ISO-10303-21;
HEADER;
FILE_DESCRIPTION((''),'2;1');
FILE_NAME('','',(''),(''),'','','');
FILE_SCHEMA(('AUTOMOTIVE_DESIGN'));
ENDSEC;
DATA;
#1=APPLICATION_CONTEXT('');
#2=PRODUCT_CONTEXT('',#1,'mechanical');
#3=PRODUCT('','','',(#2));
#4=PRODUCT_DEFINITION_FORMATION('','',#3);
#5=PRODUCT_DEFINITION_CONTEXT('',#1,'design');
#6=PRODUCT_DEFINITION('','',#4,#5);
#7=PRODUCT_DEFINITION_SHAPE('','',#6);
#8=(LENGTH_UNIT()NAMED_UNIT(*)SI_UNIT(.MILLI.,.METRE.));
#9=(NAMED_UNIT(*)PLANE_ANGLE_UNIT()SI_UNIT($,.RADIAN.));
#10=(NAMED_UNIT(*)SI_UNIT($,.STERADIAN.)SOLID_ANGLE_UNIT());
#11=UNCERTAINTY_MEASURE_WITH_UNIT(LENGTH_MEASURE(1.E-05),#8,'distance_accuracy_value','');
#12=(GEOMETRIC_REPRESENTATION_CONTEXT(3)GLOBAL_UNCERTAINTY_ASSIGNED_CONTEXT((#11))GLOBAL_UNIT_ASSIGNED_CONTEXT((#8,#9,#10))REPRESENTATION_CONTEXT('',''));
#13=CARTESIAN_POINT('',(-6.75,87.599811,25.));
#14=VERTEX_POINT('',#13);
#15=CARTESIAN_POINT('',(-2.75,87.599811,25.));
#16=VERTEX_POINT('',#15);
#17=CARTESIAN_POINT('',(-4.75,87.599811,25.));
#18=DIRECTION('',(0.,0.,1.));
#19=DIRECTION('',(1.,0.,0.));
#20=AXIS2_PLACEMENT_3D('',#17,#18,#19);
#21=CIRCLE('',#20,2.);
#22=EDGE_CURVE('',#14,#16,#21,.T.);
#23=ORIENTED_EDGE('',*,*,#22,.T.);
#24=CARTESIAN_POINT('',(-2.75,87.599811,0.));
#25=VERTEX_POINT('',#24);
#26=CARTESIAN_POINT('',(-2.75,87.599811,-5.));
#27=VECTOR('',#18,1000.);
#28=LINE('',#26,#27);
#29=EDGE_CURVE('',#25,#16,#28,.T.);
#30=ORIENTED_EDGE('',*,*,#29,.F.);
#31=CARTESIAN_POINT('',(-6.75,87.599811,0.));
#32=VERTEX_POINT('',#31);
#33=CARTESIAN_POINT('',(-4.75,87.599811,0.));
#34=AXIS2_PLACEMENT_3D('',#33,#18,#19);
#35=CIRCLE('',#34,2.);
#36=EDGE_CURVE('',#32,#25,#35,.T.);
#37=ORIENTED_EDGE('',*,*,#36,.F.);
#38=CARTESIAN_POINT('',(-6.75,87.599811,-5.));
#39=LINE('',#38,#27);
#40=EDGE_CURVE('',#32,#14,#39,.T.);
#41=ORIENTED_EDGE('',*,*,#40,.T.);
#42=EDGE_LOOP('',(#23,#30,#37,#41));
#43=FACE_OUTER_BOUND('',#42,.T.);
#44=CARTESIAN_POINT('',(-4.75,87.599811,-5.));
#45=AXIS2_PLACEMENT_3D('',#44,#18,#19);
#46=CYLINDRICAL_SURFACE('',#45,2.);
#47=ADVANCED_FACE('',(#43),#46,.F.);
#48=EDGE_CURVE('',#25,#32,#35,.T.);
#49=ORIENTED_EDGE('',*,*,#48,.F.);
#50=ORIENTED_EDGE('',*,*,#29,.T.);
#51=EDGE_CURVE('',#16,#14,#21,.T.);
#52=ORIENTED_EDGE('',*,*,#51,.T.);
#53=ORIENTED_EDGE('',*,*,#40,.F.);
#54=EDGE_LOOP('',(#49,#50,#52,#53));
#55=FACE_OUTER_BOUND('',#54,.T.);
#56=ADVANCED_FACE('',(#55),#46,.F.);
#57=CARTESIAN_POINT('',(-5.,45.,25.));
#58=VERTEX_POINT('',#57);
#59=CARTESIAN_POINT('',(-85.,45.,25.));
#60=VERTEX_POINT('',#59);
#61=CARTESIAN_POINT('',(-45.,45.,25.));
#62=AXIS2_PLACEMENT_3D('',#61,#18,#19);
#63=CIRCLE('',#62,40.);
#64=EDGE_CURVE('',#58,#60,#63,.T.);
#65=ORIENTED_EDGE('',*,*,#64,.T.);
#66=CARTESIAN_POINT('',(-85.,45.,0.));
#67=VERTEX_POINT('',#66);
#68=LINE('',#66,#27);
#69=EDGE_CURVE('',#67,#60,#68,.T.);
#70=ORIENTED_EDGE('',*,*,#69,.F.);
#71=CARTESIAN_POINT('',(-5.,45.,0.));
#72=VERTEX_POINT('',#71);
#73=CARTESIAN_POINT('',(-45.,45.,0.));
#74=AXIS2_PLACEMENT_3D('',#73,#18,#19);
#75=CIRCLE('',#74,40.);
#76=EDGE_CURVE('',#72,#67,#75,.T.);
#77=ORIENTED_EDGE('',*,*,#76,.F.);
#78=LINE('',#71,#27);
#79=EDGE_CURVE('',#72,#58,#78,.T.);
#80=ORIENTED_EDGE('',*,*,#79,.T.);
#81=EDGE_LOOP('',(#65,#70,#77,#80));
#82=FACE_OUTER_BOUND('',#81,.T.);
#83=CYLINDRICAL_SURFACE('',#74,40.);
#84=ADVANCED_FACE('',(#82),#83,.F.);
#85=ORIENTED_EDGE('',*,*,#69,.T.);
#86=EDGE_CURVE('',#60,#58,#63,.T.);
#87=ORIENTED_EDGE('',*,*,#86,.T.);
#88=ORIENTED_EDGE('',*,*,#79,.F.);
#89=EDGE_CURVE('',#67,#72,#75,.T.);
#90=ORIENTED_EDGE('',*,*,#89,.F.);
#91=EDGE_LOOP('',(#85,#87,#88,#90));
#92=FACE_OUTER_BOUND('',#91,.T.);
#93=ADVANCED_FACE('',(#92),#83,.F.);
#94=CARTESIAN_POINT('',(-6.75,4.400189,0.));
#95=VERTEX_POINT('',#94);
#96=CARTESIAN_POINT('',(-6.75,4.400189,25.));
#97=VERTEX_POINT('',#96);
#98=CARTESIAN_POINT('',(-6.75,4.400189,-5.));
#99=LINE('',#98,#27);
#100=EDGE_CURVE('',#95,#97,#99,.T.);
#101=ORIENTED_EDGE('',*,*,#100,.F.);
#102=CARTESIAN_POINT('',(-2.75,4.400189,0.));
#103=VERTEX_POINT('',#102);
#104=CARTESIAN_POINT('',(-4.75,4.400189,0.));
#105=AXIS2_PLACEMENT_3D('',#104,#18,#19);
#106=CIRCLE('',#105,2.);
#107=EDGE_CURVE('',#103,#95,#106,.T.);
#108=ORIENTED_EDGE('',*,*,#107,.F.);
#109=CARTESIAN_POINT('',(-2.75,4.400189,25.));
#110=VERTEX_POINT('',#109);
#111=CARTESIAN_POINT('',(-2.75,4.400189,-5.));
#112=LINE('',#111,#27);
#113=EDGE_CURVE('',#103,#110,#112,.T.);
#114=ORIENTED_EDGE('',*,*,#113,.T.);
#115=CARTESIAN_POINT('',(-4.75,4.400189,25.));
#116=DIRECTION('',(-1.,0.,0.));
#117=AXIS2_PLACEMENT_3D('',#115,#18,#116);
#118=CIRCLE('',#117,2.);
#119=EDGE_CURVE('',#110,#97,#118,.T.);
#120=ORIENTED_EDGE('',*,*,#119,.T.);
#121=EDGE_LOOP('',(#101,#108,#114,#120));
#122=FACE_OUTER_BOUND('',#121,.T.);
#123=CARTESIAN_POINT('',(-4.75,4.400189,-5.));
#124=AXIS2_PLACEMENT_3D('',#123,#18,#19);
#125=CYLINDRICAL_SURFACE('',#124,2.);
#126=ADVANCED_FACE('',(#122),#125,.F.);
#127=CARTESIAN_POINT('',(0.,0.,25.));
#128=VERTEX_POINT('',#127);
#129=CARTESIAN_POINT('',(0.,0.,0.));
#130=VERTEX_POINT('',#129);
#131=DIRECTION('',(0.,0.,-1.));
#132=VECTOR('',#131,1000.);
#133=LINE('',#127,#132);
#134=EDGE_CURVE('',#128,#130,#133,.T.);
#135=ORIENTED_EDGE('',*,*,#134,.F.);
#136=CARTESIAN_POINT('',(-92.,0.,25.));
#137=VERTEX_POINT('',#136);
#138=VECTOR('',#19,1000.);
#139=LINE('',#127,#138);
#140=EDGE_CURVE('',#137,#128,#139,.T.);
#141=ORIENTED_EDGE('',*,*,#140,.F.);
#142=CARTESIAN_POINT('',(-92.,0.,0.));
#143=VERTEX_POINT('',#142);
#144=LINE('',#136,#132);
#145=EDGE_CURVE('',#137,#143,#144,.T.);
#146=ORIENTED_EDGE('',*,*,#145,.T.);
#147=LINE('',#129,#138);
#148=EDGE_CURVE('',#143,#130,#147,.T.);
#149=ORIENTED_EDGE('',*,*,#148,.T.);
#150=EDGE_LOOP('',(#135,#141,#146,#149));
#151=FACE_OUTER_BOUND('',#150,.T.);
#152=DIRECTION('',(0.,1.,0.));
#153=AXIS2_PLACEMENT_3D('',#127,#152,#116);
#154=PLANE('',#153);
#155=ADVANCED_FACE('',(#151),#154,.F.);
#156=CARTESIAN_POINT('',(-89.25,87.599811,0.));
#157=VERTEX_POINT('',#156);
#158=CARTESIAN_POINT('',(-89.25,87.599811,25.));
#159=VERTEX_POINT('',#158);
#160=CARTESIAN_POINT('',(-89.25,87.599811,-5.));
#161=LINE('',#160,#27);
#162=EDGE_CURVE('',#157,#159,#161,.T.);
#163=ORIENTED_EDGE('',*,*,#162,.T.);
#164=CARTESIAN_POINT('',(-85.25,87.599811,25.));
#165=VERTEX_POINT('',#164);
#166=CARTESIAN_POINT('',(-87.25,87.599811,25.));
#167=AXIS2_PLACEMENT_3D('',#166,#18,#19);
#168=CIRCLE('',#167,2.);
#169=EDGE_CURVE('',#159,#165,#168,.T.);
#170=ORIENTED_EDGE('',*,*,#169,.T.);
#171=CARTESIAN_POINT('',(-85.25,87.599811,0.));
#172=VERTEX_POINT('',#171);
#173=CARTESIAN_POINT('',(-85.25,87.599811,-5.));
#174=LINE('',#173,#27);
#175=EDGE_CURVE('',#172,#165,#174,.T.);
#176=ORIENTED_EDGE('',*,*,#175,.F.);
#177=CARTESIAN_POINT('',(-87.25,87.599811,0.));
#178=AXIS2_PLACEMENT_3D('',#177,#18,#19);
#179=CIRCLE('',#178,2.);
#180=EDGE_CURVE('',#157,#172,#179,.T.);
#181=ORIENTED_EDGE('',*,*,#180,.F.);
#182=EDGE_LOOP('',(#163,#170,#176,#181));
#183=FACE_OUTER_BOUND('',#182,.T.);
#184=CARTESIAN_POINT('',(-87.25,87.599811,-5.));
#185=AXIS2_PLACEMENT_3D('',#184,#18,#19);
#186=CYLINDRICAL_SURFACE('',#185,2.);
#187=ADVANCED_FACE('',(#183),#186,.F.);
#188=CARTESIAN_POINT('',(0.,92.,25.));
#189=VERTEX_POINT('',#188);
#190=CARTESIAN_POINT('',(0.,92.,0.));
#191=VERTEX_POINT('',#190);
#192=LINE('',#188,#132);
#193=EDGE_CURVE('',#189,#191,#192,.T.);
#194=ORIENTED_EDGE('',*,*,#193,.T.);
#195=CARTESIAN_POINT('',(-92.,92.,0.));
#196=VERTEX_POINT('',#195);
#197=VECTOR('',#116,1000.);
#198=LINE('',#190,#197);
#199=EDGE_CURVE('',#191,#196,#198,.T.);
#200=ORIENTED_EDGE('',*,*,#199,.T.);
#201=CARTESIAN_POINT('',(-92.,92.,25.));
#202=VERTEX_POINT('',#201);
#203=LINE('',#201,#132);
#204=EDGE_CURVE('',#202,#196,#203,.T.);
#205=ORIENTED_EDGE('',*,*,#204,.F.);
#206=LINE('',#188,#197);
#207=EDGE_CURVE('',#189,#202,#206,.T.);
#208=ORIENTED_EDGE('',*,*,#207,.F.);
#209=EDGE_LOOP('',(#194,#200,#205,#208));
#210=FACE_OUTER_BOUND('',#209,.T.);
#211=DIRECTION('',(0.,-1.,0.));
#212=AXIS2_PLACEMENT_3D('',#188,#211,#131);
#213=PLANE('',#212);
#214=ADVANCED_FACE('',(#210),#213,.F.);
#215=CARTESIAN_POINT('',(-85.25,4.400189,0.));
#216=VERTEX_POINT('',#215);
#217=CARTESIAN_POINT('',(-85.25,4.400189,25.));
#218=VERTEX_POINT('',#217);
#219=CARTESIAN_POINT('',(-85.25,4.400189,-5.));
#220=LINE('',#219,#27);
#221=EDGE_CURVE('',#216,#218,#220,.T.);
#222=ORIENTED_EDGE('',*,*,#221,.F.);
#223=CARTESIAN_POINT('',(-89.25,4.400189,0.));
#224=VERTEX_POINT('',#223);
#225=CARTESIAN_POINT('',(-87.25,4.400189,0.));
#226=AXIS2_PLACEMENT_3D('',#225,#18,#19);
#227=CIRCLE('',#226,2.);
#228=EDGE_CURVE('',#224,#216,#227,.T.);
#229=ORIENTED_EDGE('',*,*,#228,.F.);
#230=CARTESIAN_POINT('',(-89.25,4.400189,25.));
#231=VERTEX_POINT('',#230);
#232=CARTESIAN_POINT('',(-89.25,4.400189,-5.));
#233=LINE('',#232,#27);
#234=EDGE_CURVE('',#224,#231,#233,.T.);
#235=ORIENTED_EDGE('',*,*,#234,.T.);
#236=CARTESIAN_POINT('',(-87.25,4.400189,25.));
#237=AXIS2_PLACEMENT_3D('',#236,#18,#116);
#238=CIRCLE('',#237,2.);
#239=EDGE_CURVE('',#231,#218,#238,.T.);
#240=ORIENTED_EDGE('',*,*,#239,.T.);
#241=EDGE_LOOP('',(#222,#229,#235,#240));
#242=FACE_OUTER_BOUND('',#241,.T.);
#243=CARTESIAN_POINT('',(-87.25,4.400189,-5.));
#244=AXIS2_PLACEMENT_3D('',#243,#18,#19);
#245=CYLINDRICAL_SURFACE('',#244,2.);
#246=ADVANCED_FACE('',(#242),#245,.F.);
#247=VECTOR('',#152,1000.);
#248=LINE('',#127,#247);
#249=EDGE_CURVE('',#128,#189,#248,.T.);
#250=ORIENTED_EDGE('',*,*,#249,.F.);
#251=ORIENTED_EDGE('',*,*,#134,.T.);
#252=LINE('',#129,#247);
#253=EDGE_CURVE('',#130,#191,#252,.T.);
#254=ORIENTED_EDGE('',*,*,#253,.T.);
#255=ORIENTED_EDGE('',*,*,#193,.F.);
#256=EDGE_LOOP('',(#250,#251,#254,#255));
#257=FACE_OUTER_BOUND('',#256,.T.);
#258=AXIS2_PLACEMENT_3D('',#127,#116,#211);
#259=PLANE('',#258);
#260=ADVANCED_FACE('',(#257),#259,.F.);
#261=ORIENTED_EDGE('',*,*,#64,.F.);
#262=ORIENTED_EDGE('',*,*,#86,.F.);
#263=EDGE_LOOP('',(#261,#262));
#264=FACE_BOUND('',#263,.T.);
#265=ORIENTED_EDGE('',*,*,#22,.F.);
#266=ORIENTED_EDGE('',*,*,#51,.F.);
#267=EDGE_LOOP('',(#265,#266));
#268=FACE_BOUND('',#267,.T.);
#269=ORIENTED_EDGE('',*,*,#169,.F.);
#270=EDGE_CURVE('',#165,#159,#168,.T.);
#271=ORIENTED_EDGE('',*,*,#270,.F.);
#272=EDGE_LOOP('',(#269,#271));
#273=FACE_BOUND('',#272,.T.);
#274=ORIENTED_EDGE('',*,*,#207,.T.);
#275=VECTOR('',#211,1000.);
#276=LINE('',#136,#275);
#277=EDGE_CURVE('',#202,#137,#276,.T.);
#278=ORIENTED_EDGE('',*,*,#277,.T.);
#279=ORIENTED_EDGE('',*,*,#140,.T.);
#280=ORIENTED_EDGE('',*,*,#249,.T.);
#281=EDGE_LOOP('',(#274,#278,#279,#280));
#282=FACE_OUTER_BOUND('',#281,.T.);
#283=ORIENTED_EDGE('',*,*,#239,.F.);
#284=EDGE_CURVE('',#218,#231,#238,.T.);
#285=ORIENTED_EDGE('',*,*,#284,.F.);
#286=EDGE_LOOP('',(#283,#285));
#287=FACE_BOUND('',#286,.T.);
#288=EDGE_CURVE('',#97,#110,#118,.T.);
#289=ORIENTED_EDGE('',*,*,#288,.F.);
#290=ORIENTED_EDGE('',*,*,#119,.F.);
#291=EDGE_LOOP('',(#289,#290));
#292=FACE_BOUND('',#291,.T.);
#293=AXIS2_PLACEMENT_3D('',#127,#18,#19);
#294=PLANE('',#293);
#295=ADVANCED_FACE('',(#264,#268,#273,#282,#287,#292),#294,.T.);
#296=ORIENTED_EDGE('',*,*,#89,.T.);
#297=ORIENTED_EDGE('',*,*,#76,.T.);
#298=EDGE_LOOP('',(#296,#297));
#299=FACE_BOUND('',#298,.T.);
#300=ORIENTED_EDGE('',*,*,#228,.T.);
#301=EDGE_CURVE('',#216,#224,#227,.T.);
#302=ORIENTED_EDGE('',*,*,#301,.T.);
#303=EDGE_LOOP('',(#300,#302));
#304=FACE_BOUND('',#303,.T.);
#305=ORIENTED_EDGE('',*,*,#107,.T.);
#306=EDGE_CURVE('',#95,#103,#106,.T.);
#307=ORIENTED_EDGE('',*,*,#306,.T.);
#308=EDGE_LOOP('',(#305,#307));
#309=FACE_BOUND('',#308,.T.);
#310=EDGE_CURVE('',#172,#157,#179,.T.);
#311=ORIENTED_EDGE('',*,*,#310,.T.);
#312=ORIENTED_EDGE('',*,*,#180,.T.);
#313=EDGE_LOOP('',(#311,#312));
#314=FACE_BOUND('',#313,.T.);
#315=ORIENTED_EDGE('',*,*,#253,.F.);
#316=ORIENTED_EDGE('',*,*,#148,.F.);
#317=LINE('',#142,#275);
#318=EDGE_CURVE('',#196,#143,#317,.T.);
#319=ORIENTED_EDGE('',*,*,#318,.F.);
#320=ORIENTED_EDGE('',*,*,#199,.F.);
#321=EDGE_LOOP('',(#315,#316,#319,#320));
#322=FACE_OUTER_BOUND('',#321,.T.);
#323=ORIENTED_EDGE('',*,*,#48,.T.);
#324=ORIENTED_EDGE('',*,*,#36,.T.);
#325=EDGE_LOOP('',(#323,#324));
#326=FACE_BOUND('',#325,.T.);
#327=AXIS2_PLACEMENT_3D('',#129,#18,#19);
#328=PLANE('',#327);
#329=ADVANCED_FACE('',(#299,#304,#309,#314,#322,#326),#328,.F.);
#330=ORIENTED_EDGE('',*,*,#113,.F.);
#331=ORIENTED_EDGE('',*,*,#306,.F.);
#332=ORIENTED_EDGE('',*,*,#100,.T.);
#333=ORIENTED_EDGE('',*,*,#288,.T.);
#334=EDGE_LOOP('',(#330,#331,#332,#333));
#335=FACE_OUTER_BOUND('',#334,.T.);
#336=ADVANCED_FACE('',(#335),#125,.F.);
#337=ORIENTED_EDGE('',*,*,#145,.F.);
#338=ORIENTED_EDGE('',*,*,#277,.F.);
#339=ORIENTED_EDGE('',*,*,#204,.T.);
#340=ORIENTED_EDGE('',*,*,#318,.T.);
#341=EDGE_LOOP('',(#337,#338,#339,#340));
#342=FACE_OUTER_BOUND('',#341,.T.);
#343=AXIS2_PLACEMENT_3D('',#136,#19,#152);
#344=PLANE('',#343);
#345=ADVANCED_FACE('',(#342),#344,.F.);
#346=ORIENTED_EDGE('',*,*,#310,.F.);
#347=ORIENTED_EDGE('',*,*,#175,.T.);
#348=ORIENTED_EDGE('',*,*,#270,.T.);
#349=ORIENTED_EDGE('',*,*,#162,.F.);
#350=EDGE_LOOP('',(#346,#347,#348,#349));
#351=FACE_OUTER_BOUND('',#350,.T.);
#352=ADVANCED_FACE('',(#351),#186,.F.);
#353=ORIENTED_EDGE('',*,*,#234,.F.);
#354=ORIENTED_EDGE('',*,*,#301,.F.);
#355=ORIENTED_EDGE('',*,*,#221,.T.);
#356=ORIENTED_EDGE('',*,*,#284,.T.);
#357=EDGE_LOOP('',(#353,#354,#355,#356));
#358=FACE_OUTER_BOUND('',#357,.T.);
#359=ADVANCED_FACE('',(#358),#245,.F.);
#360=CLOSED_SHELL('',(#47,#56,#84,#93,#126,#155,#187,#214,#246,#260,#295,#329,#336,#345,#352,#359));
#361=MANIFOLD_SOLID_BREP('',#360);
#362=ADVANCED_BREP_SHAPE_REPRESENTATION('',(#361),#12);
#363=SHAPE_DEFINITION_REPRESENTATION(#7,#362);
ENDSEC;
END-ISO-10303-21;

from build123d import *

# Parameters (mm, degrees)
SKETCH1_W           = 92
SKETCH1_H           = 92
BOSS_EXTRUDE1_DEPTH = 25
SKETCH2_R           = 40
CUT_EXTRUDE1_DEPTH  = 25
SKETCH3_R           = 2
CUT_EXTRUDE2_DEPTH  = 30


with BuildPart() as part:
    # Sketch1 → Boss-Extrude1 (new body)
    with BuildSketch(Plane.XY):
        with Locations((-46, 46)):
            Rectangle(SKETCH1_W, SKETCH1_H)
    extrude(amount=BOSS_EXTRUDE1_DEPTH)

    # Sketch2 → Cut-Extrude1 (cut)
    with BuildSketch(Plane.XY.offset(25)):
        with Locations((-45, 45)):
            Circle(SKETCH2_R)
    extrude(amount=-CUT_EXTRUDE1_DEPTH, mode=Mode.SUBTRACT)

    # Sketch3 → Cut-Extrude2 (cut)
    with BuildSketch(Plane.XY.offset(25)):
        with Locations((-4.75, 87.599810623)):
            Circle(SKETCH3_R)
        with Locations((-87.25, 87.599810623)):
            Circle(SKETCH3_R)
        with Locations((-87.25, 4.400189377)):
            Circle(SKETCH3_R)
        with Locations((-4.75, 4.400189377)):
            Circle(SKETCH3_R)
    extrude(amount=-CUT_EXTRUDE2_DEPTH, mode=Mode.SUBTRACT)


solid = part.part
